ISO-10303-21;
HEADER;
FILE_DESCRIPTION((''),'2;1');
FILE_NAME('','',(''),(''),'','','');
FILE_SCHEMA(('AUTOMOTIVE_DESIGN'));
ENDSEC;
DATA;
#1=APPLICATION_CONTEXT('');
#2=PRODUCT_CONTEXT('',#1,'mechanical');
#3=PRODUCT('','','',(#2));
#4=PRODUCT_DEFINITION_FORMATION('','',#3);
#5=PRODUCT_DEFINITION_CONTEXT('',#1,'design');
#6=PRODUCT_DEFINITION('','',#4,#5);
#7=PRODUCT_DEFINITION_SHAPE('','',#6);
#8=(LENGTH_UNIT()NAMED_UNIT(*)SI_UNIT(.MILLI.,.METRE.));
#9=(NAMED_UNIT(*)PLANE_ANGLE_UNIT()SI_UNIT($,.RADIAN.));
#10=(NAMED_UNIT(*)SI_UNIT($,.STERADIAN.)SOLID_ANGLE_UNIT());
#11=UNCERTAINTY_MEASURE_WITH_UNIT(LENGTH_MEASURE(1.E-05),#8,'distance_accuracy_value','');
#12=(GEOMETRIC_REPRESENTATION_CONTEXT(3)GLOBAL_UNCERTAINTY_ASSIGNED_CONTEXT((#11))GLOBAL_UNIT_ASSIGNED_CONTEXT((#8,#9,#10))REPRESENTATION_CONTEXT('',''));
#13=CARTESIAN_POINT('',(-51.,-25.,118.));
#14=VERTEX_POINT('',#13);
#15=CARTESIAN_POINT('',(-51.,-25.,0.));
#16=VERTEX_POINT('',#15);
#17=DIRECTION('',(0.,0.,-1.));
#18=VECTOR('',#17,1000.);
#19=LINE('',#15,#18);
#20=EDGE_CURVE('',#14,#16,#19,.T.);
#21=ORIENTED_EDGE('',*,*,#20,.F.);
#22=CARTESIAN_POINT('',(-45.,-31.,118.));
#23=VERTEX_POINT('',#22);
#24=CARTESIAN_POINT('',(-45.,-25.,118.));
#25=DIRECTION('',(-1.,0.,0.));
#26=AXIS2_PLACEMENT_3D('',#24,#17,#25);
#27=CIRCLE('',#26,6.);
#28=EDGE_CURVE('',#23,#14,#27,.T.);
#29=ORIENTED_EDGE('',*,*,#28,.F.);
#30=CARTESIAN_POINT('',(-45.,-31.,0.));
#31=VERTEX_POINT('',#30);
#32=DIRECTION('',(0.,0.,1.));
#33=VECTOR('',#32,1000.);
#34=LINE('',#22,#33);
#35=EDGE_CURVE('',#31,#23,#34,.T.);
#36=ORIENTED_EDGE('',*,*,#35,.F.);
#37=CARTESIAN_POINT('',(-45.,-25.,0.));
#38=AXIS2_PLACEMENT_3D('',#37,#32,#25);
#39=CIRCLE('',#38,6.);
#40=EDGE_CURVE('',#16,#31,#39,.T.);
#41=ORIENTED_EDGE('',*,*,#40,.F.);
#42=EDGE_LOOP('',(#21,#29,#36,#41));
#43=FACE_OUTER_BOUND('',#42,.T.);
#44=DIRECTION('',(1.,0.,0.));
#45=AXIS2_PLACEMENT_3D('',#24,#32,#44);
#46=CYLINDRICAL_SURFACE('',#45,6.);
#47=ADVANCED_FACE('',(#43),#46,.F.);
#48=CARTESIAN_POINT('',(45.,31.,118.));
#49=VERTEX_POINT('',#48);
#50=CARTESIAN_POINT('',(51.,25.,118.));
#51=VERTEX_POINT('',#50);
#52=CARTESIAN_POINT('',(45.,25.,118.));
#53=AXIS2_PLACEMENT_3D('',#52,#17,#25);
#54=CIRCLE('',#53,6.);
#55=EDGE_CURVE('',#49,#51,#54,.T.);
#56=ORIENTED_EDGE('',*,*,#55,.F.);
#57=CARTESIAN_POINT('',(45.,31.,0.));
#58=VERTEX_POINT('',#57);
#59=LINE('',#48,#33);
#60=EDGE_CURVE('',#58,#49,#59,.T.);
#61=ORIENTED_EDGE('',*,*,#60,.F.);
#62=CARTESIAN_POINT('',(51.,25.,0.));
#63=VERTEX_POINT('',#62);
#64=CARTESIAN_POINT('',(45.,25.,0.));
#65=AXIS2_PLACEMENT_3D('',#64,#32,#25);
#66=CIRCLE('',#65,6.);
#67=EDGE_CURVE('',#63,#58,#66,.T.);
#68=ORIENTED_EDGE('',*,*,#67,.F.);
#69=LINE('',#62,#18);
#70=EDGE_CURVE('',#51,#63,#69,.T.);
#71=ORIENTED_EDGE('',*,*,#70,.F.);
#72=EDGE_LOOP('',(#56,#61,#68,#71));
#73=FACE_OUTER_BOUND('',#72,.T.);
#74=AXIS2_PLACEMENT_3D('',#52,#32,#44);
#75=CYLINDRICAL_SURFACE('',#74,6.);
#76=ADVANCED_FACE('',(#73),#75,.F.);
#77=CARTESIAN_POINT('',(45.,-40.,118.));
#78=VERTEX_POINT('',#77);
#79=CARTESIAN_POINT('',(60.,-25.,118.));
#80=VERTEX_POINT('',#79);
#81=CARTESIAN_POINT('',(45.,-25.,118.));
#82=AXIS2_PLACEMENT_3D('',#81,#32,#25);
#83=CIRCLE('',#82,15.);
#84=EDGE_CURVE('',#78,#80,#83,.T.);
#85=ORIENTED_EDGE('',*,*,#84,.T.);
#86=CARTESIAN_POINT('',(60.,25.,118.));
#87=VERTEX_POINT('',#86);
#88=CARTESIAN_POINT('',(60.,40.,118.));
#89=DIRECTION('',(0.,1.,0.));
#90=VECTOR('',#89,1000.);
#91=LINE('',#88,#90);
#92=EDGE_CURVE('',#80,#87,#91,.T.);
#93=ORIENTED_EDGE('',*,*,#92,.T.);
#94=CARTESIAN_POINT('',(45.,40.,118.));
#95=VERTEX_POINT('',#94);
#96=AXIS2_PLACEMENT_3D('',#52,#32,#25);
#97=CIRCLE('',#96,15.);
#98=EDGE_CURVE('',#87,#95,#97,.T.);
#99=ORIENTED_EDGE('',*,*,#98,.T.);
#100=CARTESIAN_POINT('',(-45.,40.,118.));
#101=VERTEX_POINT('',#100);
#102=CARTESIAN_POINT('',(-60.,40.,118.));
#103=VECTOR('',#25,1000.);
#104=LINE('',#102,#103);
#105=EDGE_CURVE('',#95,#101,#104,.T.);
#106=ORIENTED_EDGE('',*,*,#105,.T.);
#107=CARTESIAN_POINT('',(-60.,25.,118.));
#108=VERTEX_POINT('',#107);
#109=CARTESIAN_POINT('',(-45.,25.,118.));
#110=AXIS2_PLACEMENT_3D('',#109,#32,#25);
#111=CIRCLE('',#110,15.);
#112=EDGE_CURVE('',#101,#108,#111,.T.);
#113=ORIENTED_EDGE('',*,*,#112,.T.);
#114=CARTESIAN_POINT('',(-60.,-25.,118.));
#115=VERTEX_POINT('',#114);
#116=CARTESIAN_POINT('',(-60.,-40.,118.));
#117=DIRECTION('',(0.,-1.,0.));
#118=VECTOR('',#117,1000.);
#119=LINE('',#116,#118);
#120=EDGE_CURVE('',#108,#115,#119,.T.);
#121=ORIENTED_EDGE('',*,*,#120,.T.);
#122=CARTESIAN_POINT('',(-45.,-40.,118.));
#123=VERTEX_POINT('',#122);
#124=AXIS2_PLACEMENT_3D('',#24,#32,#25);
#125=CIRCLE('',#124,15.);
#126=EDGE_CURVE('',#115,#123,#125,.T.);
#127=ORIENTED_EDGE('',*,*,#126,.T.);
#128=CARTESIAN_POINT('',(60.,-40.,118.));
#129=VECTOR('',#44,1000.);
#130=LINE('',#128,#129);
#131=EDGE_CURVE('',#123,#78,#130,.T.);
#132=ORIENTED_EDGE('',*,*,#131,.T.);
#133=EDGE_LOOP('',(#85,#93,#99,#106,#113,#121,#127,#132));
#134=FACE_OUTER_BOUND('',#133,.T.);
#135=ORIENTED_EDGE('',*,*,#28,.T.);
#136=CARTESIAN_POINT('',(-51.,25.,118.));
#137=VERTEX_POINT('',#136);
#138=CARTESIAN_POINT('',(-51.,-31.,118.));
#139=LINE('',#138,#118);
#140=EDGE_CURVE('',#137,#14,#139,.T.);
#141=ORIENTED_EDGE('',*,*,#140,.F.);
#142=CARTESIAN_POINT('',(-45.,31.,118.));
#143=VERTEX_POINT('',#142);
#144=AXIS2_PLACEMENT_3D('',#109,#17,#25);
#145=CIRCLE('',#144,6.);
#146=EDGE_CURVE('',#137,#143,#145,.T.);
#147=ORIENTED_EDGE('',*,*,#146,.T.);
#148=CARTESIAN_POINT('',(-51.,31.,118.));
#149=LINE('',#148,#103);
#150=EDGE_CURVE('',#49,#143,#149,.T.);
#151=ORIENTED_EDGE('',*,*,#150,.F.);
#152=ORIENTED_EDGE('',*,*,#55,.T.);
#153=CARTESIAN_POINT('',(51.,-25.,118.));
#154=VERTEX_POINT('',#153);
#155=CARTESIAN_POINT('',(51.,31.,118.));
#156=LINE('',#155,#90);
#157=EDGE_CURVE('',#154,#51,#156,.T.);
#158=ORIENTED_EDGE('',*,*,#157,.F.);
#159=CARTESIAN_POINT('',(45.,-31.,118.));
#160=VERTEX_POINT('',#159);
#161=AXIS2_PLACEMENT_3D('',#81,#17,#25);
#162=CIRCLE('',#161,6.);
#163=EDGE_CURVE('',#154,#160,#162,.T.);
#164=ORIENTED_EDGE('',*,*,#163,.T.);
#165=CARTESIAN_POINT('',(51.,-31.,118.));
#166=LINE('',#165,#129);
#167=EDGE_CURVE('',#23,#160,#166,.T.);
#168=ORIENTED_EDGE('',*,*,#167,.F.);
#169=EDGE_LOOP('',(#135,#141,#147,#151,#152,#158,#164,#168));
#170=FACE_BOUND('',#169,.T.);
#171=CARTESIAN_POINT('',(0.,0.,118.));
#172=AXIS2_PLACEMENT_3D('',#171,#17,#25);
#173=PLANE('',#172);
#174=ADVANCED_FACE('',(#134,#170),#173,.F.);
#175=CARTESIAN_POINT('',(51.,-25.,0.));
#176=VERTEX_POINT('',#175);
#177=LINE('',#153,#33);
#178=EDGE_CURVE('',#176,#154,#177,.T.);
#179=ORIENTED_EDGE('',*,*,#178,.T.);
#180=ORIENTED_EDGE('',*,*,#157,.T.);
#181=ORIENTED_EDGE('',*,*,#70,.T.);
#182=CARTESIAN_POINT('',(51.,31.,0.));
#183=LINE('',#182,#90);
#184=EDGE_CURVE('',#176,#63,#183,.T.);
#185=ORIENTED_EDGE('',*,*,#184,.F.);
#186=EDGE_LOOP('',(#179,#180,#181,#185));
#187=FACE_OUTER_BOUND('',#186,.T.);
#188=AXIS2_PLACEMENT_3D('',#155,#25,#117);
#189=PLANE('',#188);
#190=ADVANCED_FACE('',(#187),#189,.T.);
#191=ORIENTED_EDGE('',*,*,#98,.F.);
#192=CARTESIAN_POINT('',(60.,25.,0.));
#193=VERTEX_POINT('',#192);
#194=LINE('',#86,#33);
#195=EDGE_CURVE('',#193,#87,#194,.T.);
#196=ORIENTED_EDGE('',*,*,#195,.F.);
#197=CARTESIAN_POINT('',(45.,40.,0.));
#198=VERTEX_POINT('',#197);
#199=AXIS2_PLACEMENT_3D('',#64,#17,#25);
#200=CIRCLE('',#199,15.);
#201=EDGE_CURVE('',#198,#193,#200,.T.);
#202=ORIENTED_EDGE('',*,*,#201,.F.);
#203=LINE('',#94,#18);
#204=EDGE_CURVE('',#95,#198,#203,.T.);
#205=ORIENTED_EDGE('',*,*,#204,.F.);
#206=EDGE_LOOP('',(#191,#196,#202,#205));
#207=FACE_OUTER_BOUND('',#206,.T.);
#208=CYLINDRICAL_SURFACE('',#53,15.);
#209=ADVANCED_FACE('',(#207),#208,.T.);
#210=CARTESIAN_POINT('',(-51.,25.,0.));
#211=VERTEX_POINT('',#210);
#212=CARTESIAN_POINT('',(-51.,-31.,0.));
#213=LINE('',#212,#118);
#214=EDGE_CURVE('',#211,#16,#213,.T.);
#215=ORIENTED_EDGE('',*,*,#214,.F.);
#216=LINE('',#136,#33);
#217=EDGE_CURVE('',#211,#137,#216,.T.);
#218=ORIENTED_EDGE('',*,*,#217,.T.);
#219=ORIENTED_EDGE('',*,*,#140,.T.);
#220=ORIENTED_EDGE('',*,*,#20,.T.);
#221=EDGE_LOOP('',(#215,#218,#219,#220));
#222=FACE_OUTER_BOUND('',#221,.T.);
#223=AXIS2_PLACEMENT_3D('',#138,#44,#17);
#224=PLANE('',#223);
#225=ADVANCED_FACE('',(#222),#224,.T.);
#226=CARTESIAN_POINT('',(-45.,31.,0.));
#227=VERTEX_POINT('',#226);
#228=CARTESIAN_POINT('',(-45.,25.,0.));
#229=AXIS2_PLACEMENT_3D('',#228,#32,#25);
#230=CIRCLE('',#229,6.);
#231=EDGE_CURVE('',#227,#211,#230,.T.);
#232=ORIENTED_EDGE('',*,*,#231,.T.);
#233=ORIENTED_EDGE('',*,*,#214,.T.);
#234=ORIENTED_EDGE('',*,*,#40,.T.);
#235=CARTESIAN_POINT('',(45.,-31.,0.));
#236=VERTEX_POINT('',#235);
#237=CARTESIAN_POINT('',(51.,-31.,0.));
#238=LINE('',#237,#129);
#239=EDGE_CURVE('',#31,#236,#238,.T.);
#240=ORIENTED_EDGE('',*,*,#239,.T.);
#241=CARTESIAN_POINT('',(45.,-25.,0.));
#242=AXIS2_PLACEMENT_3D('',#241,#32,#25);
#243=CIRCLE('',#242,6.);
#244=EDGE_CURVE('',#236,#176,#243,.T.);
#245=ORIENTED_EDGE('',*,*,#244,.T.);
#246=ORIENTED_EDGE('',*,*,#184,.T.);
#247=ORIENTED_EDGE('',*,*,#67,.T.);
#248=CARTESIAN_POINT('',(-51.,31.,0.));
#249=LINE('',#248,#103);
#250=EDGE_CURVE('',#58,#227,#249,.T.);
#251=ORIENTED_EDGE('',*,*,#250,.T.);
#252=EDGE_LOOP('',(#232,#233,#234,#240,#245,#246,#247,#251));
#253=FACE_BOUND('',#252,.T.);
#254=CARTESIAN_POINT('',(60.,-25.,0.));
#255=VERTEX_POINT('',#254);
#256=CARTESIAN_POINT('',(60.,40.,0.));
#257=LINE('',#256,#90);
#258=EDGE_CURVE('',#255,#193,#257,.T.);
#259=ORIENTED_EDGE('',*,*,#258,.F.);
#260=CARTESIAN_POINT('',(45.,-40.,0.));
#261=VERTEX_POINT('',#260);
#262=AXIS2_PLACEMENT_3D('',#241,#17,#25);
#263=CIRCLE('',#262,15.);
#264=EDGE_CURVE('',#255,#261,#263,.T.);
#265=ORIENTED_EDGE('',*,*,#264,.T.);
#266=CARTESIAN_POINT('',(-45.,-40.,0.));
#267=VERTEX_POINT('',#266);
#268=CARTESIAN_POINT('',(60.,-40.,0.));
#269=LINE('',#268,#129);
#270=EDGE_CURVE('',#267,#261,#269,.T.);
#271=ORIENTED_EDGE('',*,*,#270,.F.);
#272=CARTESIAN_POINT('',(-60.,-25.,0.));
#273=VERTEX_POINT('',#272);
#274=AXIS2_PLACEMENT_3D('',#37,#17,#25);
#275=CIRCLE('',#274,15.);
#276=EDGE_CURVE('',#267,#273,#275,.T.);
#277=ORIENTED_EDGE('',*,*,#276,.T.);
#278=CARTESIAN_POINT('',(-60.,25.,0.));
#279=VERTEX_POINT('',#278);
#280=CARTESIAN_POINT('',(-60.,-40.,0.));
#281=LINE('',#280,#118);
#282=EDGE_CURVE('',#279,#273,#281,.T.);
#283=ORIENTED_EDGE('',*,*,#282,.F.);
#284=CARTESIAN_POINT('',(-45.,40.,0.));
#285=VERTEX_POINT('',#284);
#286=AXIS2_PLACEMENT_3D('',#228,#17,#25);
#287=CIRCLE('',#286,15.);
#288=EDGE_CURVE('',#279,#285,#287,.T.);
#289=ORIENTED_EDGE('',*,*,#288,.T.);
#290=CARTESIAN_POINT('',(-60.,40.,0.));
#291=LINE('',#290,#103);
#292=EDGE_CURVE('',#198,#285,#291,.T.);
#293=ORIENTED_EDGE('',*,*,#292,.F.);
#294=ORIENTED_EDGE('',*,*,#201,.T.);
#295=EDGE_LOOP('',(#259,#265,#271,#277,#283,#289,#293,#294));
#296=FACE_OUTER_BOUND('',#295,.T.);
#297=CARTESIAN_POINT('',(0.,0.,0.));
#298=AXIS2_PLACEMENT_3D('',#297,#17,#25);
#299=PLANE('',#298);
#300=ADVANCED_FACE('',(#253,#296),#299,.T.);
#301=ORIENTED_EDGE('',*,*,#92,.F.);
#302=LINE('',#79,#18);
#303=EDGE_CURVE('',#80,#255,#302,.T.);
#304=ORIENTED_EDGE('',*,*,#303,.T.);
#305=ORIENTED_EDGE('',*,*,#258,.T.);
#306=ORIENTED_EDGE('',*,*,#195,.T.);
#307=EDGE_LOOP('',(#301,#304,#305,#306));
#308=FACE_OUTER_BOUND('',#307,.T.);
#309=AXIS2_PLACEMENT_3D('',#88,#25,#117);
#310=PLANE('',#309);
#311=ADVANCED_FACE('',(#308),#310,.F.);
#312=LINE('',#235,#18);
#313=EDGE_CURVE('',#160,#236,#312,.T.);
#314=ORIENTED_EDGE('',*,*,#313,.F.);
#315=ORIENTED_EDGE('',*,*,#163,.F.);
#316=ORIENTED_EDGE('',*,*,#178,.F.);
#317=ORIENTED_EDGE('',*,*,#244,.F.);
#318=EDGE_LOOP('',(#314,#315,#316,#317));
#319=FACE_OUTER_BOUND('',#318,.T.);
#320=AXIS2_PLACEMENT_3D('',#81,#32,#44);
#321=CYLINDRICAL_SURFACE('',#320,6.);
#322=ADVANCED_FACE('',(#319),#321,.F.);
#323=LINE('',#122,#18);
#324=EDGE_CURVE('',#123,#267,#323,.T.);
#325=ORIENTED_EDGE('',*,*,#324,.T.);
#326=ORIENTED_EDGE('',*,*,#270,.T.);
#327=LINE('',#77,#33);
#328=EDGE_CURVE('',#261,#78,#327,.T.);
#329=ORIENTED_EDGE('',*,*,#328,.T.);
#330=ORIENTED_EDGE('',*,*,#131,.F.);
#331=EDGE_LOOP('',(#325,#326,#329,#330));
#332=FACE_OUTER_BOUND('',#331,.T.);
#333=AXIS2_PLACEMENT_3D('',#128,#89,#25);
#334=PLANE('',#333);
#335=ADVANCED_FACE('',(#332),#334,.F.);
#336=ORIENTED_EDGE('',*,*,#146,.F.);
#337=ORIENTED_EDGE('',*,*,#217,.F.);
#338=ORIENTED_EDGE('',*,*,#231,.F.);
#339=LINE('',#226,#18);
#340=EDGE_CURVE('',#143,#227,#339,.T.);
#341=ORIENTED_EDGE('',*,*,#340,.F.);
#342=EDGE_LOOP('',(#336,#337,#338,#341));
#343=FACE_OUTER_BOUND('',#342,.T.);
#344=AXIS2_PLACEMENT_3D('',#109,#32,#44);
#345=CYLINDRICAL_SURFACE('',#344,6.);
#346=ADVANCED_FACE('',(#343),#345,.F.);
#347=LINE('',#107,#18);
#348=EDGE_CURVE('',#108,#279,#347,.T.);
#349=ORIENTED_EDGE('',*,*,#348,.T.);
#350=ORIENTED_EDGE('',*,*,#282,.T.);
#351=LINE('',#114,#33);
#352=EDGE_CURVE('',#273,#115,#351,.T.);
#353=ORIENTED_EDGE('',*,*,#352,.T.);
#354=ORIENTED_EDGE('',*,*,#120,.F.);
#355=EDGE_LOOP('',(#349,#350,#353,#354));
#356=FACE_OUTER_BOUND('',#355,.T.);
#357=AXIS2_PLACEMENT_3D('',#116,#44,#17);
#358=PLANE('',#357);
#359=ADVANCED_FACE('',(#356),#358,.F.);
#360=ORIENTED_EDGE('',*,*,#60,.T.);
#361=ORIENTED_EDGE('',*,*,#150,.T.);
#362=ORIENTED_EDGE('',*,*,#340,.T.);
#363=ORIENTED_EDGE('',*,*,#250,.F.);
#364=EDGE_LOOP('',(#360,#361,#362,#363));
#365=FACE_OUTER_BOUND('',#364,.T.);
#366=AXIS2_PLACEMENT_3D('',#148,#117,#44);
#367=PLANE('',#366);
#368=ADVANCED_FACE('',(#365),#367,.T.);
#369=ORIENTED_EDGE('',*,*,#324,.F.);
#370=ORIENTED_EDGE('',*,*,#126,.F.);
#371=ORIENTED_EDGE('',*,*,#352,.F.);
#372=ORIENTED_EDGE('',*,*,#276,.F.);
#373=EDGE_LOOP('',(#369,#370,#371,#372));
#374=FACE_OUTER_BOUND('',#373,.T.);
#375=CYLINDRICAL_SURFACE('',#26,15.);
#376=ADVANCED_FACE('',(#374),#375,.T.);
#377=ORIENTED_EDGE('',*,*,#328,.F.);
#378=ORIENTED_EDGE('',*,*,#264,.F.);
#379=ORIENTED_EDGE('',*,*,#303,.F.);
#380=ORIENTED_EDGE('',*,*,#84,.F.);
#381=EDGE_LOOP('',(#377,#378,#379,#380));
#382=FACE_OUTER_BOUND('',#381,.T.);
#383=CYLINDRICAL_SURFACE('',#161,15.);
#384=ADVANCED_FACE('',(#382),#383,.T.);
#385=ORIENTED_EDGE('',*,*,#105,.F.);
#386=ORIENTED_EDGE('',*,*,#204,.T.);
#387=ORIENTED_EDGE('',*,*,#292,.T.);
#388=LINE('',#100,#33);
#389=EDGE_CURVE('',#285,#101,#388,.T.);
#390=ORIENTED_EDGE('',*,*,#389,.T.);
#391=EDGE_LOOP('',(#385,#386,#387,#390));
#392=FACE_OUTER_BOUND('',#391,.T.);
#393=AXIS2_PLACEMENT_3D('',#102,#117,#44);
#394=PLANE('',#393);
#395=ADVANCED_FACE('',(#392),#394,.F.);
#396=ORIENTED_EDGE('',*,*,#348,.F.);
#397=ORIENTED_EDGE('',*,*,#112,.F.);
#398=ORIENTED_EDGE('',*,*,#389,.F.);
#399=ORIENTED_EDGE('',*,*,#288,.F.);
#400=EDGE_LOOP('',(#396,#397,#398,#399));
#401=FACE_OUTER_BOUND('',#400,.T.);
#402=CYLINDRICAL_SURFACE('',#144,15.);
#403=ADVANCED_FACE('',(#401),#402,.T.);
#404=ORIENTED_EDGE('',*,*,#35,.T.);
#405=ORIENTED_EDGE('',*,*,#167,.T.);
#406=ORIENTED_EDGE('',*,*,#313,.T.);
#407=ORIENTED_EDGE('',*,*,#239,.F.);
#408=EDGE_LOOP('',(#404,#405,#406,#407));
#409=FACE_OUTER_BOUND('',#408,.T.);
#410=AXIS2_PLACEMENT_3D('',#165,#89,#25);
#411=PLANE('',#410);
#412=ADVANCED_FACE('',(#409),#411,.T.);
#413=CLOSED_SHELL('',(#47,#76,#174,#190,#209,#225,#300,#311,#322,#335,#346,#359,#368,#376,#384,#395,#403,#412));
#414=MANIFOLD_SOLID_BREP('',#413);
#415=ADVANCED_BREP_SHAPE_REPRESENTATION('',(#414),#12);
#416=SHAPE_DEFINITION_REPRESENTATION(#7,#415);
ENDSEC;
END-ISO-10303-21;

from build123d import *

# Parameters (mm, degrees)
SKETCH_1_W      = 120
SKETCH_1_H      = 80
SKETCH_1_W_2    = 102
SKETCH_1_H_2    = 62
EXTRUDE_1_DEPTH = 118
FILLET_1_R      = 15
FILLET_2_R      = 6


with BuildPart() as part:
    # 草图1 → 凸台-拉伸1 (new body)
    with BuildSketch(Plane.XY):
        Rectangle(SKETCH_1_W, SKETCH_1_H)
        Rectangle(SKETCH_1_W_2, SKETCH_1_H_2, mode=Mode.SUBTRACT)
    extrude(amount=EXTRUDE_1_DEPTH)

    # 圆角1
    fillet_1_edges = [part.edges().sort_by_distance(p)[0] for p in [
        (-60, 40, 59),
        (60, 40, 59),
        (60, -40, 59),
        (-60, -40, 59),
    ]]
    fillet(fillet_1_edges, radius=FILLET_1_R)

    # 圆角2
    fillet_2_edges = [part.edges().sort_by_distance(p)[0] for p in [
        (-51, 31, 59),
        (-51, -31, 59),
        (51, -31, 59),
        (51, 31, 59),
    ]]
    fillet(fillet_2_edges, radius=FILLET_2_R)


solid = part.part
